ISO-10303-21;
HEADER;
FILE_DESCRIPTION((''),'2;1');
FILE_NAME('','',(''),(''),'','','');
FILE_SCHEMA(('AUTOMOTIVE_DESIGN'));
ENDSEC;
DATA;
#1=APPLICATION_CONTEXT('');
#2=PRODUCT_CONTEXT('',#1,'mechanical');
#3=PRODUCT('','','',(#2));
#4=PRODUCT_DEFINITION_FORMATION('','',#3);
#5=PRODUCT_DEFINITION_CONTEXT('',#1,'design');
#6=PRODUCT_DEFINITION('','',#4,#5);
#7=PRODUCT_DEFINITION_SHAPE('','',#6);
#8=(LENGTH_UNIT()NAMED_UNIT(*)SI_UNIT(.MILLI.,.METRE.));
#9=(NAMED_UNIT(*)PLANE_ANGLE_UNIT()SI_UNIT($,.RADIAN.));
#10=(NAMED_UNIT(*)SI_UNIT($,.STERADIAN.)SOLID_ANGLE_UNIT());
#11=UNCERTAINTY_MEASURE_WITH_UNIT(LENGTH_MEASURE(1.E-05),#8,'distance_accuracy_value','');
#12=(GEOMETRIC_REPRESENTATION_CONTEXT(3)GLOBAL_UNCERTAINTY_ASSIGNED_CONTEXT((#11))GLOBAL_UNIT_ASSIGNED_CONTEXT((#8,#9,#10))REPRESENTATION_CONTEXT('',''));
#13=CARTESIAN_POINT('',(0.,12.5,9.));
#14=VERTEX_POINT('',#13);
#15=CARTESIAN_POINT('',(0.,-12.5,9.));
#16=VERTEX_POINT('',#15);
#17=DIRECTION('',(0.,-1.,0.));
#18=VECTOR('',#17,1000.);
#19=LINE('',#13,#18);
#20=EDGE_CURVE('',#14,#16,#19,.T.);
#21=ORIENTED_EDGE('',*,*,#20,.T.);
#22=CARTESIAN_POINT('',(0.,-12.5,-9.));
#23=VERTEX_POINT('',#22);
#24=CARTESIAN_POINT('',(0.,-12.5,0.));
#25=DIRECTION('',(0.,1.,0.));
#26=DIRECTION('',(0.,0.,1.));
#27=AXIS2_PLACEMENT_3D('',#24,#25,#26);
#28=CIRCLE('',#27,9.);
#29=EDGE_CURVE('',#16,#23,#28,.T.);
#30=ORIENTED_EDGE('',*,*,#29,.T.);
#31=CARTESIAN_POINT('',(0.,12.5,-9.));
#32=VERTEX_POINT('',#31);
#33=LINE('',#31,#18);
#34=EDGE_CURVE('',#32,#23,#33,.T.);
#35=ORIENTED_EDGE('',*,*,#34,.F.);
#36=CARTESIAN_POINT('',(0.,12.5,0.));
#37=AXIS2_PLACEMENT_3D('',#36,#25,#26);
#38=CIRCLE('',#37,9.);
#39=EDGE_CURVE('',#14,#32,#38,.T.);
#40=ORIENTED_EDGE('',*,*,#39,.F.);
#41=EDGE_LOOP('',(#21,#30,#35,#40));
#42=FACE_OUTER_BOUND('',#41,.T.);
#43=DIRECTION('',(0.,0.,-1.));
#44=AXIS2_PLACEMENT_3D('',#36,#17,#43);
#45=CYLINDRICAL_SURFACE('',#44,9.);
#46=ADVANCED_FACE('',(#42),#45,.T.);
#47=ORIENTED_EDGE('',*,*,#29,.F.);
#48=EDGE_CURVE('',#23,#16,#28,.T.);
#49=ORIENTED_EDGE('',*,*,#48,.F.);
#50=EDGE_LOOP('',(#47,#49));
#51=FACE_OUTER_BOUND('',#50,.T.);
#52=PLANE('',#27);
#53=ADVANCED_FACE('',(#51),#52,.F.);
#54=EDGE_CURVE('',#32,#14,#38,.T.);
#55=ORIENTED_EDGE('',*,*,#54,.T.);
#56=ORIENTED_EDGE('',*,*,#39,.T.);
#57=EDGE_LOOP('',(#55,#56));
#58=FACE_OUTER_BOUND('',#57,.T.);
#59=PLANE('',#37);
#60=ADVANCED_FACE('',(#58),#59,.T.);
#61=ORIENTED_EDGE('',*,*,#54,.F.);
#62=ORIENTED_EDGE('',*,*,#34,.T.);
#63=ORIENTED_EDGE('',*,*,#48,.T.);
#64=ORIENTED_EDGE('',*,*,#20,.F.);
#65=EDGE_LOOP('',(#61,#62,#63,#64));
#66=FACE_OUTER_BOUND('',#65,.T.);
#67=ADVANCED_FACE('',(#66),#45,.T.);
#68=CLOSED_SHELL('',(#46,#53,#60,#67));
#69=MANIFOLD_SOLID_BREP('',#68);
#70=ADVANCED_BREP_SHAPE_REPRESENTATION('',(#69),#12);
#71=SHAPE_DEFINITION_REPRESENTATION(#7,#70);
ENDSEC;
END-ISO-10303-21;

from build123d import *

# Parameters (mm, degrees)
SKETCH_1_R      = 9
EXTRUDE_1_DEPTH = 12.5


with BuildPart() as part:
    # 草图1 → 凸台-拉伸1 (new, symmetric)
    with BuildSketch(Plane(origin=(0, 0, 0), x_dir=(1, 0, 0), z_dir=(0, 1, 0))):
        with Locations(Location((0, 0, 0), (0, 0, 270))):
            Circle(SKETCH_1_R)
    extrude(amount=EXTRUDE_1_DEPTH, both=True)


solid = part.part
